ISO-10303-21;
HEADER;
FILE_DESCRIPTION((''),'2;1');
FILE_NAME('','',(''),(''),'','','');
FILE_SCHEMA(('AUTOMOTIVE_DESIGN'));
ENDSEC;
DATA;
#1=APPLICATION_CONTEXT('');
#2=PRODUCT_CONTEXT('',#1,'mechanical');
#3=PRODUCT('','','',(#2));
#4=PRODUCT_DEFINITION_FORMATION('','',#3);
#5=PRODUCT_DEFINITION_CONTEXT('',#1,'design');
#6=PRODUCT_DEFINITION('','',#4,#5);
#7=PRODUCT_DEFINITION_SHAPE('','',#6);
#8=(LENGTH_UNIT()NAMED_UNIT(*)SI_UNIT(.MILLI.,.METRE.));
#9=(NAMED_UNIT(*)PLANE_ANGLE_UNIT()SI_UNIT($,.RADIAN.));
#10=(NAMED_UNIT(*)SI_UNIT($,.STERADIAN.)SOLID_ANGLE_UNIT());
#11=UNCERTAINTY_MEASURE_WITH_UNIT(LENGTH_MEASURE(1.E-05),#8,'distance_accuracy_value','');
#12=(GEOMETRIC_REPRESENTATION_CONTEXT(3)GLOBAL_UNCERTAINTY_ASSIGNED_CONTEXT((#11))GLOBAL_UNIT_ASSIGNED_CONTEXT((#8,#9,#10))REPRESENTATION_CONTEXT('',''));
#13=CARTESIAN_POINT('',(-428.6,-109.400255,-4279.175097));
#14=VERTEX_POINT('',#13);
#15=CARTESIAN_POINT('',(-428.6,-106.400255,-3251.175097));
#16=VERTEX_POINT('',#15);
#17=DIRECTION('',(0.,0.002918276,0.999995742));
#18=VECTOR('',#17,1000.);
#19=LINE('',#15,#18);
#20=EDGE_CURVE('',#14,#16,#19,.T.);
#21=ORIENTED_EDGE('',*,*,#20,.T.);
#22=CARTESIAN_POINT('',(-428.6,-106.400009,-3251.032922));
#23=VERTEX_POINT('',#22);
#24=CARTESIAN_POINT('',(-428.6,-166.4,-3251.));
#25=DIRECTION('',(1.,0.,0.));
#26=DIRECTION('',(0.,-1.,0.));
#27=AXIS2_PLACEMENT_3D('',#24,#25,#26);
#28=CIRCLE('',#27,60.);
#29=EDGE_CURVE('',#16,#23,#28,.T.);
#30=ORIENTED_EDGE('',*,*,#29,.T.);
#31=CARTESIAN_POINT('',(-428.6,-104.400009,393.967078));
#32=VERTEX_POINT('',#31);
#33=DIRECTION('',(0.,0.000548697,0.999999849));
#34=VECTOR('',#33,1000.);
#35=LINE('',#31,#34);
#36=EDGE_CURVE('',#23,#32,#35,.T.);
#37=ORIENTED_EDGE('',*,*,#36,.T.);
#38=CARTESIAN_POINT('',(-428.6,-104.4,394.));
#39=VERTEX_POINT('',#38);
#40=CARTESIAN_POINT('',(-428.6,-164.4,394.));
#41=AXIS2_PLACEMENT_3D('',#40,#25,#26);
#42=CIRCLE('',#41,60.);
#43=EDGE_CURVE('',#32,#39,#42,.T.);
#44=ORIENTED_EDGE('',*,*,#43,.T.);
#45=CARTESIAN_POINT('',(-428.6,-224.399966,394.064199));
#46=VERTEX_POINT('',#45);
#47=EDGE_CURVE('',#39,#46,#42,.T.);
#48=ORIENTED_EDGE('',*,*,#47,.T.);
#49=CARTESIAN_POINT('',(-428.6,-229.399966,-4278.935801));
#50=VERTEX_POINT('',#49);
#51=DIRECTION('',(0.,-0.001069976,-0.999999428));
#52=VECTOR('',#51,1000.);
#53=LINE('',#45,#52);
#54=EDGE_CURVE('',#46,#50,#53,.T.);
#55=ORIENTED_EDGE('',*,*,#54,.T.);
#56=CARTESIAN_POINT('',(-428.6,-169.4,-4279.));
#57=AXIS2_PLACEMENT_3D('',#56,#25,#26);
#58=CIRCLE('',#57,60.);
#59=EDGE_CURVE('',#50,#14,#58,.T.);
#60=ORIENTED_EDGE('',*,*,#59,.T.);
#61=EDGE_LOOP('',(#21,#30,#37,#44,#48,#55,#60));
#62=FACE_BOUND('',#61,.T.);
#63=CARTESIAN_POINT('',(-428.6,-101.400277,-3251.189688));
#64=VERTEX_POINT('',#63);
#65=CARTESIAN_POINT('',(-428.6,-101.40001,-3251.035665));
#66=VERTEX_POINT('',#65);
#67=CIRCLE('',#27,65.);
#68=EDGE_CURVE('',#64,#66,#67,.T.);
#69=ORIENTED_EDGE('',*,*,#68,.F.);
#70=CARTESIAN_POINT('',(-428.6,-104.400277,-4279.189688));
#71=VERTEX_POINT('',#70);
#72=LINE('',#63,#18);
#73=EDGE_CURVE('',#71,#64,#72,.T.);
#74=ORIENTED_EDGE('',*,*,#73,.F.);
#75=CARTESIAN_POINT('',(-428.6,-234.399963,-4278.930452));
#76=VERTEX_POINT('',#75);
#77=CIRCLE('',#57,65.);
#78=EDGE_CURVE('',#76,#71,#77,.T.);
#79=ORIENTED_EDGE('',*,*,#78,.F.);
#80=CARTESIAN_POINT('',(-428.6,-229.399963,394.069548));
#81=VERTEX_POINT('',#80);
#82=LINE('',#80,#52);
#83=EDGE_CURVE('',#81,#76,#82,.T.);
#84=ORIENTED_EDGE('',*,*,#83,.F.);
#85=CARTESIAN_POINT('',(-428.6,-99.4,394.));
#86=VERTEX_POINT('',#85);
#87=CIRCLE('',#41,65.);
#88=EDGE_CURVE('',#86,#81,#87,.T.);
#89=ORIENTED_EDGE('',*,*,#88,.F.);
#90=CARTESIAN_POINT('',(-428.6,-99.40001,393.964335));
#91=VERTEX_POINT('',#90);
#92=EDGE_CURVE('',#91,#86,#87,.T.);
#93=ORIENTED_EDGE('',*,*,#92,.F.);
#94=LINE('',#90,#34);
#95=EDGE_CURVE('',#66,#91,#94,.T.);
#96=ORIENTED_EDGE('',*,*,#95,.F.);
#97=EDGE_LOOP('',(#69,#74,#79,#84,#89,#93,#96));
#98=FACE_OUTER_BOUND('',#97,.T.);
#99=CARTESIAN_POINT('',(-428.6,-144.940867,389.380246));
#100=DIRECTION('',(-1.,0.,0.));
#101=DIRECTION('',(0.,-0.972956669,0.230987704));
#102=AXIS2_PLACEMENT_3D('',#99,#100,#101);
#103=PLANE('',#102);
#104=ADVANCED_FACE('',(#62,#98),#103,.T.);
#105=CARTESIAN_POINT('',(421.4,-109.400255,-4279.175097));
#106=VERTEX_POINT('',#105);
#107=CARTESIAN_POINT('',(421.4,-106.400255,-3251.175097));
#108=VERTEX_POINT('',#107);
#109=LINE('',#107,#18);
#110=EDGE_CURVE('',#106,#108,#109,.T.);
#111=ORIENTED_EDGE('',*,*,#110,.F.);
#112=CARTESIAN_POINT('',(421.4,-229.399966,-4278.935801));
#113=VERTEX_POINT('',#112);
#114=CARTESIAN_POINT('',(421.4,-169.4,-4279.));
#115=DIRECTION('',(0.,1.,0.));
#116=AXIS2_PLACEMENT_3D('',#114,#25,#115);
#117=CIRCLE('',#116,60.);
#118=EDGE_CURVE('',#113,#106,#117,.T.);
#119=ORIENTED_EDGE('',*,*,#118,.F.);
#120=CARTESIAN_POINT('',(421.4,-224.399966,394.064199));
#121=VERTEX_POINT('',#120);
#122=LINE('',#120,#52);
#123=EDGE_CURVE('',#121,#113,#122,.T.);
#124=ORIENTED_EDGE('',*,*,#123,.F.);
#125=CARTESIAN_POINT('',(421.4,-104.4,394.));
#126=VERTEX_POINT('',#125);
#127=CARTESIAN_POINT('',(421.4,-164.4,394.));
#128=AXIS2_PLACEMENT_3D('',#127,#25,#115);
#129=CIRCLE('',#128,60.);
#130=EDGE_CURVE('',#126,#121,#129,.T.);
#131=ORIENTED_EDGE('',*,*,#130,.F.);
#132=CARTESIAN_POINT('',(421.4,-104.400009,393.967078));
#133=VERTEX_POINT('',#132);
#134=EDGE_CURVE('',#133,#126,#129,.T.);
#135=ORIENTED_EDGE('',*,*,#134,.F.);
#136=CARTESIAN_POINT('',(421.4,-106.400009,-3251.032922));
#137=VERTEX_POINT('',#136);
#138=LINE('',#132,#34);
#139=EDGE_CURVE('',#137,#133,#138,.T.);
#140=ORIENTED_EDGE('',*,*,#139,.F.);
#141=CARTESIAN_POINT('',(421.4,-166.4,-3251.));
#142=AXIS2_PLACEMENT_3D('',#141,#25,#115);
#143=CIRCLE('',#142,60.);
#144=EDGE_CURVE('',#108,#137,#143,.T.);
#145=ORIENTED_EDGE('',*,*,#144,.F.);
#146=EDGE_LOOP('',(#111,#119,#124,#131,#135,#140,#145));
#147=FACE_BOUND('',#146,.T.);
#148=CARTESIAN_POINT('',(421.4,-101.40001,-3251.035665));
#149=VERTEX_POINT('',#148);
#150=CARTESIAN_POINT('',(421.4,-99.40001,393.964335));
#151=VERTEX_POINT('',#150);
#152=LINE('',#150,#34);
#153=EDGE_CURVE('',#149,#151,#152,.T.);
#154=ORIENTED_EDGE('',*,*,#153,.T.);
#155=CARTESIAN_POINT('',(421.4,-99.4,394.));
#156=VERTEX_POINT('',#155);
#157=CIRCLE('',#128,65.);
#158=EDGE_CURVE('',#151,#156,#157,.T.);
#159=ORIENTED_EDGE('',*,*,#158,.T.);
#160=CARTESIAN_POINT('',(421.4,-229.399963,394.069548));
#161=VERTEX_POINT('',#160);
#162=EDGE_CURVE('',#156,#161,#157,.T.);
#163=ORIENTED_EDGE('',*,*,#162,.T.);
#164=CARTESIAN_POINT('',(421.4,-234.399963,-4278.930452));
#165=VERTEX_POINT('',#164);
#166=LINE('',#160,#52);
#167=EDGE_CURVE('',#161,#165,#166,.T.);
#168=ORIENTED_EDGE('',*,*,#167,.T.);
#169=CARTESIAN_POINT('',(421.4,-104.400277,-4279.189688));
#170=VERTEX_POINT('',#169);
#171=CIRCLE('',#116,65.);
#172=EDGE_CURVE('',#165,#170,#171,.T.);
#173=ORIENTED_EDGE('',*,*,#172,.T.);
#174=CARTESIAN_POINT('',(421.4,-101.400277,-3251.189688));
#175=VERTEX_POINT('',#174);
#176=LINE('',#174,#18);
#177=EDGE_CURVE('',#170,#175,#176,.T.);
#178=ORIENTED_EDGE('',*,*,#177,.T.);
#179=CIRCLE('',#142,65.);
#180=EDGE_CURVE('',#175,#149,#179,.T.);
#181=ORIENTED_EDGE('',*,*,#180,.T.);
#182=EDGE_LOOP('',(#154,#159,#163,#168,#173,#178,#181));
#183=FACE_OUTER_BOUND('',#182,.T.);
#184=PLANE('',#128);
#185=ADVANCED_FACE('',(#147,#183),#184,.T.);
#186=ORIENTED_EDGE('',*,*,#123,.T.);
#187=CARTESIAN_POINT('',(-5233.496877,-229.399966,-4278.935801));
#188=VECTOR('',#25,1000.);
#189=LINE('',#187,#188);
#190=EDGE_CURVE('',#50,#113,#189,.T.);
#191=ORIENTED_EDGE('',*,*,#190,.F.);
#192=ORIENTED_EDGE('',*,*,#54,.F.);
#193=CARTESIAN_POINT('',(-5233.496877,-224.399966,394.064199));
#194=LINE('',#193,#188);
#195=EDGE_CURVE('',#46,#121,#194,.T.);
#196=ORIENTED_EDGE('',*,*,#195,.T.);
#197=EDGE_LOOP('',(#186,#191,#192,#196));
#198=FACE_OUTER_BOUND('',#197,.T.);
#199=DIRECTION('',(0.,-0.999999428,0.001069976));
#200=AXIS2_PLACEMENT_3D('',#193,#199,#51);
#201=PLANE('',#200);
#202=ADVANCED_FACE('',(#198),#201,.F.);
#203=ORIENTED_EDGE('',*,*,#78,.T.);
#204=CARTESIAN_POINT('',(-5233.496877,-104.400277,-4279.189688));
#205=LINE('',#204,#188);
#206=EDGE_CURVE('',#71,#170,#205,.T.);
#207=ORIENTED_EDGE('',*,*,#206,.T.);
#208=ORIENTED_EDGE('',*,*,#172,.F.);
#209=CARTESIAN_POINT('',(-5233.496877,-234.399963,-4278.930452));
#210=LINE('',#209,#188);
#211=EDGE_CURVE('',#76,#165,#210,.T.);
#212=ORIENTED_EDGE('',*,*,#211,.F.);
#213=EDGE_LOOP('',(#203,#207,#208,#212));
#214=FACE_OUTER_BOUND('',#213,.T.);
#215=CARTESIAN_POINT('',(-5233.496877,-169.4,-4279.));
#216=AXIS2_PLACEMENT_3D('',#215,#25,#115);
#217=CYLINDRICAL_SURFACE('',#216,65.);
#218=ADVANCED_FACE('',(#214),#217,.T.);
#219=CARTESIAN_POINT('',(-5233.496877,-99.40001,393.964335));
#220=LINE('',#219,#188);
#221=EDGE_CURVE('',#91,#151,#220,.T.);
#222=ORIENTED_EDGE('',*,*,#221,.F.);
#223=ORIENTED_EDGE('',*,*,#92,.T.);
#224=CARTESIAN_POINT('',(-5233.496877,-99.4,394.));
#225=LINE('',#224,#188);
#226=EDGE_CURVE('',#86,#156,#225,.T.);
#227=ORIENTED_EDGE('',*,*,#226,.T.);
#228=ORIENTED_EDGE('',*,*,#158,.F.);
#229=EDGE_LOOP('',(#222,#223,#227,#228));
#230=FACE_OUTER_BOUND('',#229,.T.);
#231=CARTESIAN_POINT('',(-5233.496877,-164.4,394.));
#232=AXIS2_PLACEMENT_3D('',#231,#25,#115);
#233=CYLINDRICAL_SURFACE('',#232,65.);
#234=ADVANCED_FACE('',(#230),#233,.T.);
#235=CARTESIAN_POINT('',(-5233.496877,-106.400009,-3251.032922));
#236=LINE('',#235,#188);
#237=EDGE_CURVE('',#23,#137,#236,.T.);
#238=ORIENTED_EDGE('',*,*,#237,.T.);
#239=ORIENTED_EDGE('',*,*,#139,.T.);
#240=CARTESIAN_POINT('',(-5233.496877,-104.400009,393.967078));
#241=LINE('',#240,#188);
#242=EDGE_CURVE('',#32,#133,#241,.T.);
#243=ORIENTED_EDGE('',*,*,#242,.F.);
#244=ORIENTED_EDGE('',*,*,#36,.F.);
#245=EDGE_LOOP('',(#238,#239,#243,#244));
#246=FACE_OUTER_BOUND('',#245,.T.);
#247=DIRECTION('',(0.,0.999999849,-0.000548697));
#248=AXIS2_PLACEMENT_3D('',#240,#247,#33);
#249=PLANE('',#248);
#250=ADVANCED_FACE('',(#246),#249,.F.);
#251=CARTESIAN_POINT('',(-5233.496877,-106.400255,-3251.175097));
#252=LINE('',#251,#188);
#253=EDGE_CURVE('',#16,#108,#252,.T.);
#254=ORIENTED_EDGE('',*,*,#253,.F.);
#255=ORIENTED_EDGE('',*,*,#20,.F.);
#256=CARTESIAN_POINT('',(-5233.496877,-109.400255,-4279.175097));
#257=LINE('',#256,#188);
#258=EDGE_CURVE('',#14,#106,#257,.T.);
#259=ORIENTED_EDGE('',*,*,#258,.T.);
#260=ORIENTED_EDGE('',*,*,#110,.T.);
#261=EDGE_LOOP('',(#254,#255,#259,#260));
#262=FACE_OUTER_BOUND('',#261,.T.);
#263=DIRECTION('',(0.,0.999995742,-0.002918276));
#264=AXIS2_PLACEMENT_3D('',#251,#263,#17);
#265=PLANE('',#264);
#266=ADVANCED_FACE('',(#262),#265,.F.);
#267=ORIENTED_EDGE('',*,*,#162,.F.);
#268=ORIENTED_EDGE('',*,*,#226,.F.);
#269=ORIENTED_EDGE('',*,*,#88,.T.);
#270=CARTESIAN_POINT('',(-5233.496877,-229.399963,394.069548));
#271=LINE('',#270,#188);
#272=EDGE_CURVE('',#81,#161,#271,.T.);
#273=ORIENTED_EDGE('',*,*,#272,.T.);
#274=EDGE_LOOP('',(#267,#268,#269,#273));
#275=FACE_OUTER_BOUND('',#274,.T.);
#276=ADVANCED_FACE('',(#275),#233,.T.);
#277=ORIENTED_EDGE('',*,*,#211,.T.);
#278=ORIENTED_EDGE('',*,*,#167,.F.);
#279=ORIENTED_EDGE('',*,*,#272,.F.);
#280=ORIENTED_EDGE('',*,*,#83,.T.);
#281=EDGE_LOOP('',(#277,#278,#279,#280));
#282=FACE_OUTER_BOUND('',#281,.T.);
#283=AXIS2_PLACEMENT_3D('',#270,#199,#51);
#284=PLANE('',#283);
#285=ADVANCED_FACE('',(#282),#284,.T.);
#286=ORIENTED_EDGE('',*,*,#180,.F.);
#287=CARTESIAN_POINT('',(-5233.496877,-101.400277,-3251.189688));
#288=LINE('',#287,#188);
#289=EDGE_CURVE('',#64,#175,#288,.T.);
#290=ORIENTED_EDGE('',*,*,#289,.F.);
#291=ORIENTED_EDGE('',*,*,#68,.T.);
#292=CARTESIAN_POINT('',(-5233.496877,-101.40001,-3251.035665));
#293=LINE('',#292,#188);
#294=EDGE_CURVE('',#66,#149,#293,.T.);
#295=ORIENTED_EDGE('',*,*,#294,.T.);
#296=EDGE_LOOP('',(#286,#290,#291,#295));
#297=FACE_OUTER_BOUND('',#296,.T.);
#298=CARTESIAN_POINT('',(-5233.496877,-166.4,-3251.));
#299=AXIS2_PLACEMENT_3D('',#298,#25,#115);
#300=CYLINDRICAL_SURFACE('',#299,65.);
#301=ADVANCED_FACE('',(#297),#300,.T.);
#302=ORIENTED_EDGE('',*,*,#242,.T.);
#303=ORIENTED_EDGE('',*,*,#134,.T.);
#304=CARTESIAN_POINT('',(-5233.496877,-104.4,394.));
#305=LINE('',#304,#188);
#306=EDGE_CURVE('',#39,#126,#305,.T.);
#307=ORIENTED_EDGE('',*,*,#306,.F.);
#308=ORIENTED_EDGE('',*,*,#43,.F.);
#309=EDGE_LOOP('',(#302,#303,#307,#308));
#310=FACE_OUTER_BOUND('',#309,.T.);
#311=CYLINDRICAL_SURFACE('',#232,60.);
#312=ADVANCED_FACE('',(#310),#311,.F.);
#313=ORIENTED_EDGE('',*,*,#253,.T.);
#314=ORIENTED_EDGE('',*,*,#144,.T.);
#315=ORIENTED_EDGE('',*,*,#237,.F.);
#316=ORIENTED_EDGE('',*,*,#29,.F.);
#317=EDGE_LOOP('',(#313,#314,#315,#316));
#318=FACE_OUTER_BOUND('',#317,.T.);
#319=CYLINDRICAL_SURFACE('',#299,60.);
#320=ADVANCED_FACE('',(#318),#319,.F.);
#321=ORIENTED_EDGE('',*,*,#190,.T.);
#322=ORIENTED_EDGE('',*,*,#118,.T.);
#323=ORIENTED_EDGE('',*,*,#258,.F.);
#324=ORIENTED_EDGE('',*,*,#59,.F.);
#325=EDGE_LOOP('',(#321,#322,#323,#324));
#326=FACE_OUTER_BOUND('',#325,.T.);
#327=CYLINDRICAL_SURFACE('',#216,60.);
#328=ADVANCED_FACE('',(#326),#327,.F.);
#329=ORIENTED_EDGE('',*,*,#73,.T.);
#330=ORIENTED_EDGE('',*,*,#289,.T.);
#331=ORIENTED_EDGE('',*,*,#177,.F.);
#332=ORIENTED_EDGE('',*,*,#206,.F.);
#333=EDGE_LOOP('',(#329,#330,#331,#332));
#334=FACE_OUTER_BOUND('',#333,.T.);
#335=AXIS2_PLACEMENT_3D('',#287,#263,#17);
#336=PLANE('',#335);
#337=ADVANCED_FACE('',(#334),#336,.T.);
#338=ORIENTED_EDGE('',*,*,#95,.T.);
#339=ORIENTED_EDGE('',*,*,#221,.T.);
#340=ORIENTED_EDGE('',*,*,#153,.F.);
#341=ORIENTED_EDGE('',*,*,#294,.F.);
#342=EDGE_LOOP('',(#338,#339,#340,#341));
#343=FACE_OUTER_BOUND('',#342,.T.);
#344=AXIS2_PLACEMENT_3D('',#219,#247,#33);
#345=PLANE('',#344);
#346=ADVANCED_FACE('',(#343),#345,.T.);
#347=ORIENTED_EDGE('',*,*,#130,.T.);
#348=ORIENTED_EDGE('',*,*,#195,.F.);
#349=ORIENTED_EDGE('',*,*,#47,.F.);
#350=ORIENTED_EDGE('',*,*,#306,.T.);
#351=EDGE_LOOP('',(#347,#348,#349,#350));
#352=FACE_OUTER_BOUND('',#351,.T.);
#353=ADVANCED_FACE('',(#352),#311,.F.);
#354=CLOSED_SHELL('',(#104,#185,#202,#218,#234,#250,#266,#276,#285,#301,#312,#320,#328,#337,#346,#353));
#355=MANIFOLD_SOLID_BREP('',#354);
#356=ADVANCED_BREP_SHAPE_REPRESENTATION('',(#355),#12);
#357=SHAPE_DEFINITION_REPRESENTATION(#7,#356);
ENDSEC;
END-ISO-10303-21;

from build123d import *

# Parameters (mm, degrees)
EXTRUDE_1_DEPTH = 850


with BuildPart() as part:
    # 草图1 → 凸台-拉伸1 (new body)
    with BuildSketch(Plane(origin=(421.4, 0, 0), x_dir=(0, 0, -1), z_dir=(1, 0, 0))):
        with BuildLine():
            Line((-393.96433471, -99.400009785), (3251.03566529, -101.400009785))
            ThreePointArc((3251.03566529, -101.400009785), (3251.112676678, -101.400097662), (3251.189687908, -101.400276781))
            Line((3251.189687908, -101.400276781), (4279.189687908, -104.400276781))
            ThreePointArc((4279.189687908, -104.400276781), (4343.999870762, -169.529618225), (4278.93045157, -234.399962792))
            Line((4278.93045157, -234.399962792), (-394.06954843, -229.399962792))
            ThreePointArc((-394.06954843, -229.399962792), (-458.999978712, -164.347393138), (-393.96433471, -99.400009785))
        make_face()
        with BuildLine():
            Line((-393.967078194, -104.400009032), (3251.032921806, -106.400009032))
            ThreePointArc((3251.032921806, -106.400009032), (3251.104009241, -106.400090149), (3251.175096531, -106.400255491))
            Line((3251.175096531, -106.400255491), (4279.175096531, -109.400255491))
            ThreePointArc((4279.175096531, -109.400255491), (4338.999880704, -169.519647592), (4278.935801449, -229.399965655))
            Line((4278.935801449, -229.399965655), (-394.064198551, -224.399965655))
            ThreePointArc((-394.064198551, -224.399965655), (-453.999980349, -164.35143982), (-393.967078194, -104.400009032))
        make_face(mode=Mode.SUBTRACT)
    extrude(amount=-EXTRUDE_1_DEPTH)


solid = part.part
